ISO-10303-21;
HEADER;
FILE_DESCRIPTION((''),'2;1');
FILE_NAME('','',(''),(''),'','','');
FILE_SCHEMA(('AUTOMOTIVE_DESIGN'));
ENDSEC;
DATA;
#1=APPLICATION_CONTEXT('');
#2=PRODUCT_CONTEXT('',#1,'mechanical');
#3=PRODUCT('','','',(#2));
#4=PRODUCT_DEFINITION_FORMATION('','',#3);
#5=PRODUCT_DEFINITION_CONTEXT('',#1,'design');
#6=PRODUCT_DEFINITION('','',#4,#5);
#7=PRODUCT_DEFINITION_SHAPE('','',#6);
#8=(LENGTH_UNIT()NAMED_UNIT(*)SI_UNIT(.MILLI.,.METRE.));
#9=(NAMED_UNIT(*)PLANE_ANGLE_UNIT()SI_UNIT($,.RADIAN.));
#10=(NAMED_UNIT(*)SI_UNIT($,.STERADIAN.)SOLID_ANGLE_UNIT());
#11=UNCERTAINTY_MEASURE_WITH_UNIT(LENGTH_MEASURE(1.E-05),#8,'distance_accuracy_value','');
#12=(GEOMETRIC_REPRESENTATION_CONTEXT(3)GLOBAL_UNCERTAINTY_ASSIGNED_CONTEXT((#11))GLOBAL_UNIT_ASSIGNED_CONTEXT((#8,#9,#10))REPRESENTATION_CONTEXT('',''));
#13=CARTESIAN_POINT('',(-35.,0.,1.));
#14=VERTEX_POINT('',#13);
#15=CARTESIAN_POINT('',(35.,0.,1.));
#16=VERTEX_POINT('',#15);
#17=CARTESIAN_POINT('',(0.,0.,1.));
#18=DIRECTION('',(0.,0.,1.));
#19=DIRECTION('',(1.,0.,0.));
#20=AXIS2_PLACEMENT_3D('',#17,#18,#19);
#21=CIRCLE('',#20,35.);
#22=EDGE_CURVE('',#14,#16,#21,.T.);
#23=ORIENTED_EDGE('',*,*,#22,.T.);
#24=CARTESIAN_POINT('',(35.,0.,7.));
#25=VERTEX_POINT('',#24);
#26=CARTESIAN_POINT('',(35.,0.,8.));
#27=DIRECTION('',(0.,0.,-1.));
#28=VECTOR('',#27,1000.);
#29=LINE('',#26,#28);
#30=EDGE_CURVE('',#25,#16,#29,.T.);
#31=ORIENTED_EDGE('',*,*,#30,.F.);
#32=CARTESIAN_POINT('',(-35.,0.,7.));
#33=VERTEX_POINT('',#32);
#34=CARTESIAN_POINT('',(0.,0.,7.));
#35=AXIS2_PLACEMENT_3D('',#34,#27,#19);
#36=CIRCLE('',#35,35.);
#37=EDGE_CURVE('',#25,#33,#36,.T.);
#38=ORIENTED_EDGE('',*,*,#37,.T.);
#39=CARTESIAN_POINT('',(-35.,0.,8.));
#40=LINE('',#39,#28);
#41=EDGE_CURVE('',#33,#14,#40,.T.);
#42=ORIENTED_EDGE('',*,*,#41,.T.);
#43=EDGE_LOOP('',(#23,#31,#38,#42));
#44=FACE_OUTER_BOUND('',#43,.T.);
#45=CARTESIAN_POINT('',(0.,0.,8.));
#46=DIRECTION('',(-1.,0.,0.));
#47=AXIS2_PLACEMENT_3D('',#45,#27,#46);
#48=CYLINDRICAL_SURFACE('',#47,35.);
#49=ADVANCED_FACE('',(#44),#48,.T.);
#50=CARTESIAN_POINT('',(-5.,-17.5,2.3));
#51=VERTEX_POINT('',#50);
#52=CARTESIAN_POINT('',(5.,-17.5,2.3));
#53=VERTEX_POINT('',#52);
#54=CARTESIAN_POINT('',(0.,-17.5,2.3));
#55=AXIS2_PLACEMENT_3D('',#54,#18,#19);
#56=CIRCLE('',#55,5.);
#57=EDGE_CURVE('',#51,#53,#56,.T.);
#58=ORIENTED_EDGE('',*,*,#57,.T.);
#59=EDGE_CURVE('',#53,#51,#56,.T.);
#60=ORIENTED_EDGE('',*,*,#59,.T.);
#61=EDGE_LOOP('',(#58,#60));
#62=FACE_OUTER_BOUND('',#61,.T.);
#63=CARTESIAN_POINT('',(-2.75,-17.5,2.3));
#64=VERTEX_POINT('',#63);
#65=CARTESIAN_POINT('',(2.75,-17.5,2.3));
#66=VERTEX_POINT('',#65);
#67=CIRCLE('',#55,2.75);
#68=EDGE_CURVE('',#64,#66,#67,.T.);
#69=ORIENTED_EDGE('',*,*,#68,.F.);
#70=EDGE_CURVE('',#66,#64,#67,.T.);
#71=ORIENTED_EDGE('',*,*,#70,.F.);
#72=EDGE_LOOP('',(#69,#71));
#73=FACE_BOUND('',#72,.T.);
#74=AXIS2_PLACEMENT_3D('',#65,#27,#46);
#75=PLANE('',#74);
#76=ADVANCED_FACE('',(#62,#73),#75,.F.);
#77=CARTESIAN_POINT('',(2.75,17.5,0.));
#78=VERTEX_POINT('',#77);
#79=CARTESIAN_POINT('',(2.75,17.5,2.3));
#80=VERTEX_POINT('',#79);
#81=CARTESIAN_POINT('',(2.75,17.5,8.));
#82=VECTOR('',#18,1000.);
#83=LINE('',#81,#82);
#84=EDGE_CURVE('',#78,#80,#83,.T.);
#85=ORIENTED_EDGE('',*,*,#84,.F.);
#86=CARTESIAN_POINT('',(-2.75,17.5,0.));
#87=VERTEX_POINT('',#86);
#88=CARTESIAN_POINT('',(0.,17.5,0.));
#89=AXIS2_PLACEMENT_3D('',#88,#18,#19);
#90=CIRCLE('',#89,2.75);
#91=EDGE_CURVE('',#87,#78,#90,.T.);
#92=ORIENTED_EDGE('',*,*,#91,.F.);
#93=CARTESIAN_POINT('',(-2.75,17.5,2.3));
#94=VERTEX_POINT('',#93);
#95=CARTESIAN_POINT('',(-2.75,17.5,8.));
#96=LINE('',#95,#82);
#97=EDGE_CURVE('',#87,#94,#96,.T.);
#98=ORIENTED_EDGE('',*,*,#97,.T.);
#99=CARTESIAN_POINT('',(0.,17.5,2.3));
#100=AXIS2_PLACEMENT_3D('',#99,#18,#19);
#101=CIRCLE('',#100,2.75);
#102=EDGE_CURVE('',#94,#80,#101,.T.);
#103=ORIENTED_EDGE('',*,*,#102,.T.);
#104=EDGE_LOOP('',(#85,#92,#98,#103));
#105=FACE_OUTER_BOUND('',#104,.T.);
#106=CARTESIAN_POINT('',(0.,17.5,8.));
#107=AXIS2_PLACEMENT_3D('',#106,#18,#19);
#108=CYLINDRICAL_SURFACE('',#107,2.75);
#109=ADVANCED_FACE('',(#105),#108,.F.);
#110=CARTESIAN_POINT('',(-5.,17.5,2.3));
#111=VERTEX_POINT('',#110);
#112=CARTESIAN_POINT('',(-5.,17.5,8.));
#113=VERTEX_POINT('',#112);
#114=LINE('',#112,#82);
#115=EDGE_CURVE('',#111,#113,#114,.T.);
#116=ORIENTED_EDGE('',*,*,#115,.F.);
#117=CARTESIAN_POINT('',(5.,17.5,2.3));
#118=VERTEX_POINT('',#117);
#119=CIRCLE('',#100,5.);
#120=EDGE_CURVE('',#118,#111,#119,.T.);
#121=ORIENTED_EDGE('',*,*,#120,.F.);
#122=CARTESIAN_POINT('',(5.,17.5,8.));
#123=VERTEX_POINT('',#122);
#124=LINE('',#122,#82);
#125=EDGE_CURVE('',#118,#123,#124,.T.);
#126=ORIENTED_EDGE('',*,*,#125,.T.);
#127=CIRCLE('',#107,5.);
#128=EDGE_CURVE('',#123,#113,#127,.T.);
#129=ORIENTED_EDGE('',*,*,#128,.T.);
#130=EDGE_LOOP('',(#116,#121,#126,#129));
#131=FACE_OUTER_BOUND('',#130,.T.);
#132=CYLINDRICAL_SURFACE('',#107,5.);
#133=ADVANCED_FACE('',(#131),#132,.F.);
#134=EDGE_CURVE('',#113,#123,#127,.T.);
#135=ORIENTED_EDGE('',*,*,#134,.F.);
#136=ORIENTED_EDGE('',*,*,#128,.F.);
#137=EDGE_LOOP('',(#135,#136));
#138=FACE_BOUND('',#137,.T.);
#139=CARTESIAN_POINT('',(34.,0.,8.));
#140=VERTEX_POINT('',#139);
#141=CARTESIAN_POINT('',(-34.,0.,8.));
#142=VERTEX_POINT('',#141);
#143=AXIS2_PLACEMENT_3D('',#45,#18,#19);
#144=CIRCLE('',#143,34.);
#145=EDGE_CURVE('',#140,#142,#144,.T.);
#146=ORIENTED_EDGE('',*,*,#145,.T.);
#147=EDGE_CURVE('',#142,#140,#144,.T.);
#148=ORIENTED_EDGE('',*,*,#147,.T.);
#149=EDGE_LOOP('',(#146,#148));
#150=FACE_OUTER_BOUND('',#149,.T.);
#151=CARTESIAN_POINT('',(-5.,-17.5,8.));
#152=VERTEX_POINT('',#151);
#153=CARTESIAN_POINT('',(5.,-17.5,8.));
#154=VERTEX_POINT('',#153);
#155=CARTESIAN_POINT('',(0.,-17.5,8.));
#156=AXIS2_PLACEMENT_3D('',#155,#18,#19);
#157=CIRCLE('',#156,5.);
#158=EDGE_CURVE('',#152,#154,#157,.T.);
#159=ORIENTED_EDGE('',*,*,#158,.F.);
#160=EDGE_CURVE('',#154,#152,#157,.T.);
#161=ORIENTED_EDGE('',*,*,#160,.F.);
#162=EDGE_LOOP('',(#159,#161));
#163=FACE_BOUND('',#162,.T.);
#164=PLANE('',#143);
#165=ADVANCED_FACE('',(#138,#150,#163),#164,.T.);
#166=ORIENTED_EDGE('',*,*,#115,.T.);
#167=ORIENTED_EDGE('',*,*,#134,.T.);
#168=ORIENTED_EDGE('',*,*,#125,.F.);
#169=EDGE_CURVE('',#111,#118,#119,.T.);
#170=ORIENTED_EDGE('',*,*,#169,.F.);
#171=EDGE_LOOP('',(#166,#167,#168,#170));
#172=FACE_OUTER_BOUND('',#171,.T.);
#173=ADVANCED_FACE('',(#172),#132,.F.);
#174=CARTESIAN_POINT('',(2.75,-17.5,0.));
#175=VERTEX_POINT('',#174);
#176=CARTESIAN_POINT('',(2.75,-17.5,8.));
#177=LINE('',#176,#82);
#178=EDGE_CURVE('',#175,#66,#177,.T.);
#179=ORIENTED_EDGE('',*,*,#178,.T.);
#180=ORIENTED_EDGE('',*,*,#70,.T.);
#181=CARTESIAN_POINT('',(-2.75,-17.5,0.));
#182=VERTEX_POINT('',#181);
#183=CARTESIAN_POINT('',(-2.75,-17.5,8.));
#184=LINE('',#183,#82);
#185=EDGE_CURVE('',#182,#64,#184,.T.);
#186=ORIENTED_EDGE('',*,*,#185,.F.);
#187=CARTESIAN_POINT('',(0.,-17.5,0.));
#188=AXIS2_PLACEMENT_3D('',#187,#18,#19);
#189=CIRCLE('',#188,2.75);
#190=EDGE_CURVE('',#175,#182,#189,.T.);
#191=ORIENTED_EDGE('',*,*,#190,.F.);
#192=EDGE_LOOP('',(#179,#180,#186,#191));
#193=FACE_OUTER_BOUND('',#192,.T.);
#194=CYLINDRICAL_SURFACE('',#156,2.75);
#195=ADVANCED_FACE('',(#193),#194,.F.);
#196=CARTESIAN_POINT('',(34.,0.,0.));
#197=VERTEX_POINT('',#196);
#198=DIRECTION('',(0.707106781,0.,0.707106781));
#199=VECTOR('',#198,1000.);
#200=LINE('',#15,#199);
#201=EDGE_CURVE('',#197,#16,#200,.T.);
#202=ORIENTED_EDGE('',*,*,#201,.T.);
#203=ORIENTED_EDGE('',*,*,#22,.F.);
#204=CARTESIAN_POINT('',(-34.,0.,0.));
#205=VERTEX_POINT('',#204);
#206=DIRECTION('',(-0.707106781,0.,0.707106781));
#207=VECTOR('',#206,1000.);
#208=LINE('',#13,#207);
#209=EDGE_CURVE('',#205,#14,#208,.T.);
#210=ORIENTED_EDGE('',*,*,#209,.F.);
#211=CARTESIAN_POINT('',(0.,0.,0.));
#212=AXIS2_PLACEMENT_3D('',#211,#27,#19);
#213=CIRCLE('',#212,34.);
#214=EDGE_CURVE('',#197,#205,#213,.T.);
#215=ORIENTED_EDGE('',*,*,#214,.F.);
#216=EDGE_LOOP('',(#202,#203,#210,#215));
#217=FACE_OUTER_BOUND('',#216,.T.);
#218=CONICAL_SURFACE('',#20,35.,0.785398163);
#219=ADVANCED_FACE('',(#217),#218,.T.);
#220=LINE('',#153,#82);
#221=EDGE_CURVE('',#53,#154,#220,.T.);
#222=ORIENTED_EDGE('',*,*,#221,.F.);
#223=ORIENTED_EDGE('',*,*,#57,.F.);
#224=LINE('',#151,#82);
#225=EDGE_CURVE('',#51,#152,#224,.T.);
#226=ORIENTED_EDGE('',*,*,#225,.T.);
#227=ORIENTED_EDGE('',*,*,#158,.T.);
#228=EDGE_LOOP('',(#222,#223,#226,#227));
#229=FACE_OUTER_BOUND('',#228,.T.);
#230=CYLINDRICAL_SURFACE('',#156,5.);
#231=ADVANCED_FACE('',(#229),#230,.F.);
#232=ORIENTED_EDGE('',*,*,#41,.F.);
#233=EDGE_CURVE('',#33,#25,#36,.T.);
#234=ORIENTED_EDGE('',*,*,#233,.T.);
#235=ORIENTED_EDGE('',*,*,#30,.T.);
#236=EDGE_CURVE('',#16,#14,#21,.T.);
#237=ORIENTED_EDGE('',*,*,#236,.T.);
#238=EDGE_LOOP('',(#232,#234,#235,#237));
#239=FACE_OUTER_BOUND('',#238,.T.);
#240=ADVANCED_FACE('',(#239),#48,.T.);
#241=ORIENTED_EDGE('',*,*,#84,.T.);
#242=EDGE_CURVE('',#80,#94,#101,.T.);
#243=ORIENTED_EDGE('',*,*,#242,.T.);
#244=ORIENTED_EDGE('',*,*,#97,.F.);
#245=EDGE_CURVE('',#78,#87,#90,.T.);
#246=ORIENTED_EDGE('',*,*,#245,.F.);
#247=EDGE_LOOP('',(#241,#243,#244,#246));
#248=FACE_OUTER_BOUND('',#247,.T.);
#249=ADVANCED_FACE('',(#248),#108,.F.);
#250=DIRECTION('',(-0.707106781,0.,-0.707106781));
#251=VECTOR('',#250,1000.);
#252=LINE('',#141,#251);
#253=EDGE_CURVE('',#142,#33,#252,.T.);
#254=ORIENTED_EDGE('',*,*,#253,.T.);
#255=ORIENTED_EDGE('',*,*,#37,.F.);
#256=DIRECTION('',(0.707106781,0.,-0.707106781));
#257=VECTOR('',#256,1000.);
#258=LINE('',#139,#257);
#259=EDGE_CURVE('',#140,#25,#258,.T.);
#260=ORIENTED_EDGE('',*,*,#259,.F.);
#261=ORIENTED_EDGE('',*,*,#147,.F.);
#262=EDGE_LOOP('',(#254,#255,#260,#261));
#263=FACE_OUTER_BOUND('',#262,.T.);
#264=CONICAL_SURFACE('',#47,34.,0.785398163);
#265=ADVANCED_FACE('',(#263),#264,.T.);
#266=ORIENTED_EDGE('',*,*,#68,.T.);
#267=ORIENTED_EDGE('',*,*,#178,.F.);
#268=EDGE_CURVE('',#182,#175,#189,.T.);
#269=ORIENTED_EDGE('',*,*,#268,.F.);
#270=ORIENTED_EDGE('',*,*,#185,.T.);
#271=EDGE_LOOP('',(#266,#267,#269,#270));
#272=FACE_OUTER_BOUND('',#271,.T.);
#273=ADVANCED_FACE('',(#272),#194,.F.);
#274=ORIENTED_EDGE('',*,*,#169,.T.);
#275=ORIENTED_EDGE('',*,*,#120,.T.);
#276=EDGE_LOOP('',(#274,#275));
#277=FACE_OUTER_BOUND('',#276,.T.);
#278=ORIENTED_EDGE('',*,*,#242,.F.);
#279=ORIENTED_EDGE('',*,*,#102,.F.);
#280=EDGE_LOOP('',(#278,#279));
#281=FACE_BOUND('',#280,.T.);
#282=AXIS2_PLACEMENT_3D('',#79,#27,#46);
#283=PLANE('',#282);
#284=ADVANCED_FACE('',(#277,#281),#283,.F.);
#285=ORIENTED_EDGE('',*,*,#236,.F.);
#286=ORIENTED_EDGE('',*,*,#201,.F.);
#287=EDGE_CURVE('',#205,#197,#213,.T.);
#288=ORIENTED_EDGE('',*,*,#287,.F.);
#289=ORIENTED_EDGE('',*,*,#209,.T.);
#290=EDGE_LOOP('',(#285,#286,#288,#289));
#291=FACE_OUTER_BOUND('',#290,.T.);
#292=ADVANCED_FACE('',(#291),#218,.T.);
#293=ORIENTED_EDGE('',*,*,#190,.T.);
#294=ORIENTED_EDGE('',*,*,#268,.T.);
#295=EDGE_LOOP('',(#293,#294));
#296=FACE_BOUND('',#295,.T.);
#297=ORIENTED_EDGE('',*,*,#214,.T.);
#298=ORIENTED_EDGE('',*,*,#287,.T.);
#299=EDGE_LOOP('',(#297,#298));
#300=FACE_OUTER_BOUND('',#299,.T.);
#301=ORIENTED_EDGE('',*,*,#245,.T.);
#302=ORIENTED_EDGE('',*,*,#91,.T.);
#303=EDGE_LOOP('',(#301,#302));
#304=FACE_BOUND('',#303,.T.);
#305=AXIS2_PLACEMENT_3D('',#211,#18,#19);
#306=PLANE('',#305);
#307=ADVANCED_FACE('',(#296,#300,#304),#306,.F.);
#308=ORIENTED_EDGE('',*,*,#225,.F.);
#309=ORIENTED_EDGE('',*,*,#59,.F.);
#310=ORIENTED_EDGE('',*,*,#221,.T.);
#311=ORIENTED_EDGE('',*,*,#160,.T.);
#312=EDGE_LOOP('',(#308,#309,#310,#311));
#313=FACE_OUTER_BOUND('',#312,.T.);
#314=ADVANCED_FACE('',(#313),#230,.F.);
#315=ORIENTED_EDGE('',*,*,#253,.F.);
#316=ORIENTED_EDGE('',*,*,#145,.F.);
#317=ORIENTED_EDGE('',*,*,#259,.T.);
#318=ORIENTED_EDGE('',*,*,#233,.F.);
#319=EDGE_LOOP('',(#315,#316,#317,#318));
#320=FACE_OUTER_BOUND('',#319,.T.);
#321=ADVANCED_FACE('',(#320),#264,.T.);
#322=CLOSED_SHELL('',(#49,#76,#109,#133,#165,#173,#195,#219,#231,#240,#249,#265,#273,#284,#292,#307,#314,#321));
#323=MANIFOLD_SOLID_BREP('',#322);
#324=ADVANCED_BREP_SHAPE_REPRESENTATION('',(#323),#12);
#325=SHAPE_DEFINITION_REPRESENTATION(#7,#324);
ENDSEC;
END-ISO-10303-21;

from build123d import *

# Parameters (mm, degrees)
SKETCH_1_R                = 35
EXTRUDE_1_DEPTH           = 8
HOLE_WIZARD_1_D           = 5.5
HOLE_WIZARD_1_CBORE_D     = 10
HOLE_WIZARD_1_CBORE_DEPTH = 5.7
CHAMFER_1_SIZE            = 1


with BuildPart() as part:
    # 草图1 → 凸台-拉伸1 (new body)
    with BuildSketch(Plane.XY):
        Circle(SKETCH_1_R)
    extrude(amount=EXTRUDE_1_DEPTH)

    # 打孔尺寸根据内六角圆柱头螺钉的类型1 (through all)
    with Locations(Plane.XY.offset(8)):
        with Locations((0, 17.5), (0, -17.5)):
            CounterBoreHole(HOLE_WIZARD_1_D / 2, HOLE_WIZARD_1_CBORE_D / 2, HOLE_WIZARD_1_CBORE_DEPTH)

    # 倒角1
    chamfer_1_edges = [part.edges().sort_by_distance(p)[0] for p in [
        (-35, 0, 0),
        (-35, 0, 8),
    ]]
    chamfer(chamfer_1_edges, length=CHAMFER_1_SIZE)


solid = part.part
